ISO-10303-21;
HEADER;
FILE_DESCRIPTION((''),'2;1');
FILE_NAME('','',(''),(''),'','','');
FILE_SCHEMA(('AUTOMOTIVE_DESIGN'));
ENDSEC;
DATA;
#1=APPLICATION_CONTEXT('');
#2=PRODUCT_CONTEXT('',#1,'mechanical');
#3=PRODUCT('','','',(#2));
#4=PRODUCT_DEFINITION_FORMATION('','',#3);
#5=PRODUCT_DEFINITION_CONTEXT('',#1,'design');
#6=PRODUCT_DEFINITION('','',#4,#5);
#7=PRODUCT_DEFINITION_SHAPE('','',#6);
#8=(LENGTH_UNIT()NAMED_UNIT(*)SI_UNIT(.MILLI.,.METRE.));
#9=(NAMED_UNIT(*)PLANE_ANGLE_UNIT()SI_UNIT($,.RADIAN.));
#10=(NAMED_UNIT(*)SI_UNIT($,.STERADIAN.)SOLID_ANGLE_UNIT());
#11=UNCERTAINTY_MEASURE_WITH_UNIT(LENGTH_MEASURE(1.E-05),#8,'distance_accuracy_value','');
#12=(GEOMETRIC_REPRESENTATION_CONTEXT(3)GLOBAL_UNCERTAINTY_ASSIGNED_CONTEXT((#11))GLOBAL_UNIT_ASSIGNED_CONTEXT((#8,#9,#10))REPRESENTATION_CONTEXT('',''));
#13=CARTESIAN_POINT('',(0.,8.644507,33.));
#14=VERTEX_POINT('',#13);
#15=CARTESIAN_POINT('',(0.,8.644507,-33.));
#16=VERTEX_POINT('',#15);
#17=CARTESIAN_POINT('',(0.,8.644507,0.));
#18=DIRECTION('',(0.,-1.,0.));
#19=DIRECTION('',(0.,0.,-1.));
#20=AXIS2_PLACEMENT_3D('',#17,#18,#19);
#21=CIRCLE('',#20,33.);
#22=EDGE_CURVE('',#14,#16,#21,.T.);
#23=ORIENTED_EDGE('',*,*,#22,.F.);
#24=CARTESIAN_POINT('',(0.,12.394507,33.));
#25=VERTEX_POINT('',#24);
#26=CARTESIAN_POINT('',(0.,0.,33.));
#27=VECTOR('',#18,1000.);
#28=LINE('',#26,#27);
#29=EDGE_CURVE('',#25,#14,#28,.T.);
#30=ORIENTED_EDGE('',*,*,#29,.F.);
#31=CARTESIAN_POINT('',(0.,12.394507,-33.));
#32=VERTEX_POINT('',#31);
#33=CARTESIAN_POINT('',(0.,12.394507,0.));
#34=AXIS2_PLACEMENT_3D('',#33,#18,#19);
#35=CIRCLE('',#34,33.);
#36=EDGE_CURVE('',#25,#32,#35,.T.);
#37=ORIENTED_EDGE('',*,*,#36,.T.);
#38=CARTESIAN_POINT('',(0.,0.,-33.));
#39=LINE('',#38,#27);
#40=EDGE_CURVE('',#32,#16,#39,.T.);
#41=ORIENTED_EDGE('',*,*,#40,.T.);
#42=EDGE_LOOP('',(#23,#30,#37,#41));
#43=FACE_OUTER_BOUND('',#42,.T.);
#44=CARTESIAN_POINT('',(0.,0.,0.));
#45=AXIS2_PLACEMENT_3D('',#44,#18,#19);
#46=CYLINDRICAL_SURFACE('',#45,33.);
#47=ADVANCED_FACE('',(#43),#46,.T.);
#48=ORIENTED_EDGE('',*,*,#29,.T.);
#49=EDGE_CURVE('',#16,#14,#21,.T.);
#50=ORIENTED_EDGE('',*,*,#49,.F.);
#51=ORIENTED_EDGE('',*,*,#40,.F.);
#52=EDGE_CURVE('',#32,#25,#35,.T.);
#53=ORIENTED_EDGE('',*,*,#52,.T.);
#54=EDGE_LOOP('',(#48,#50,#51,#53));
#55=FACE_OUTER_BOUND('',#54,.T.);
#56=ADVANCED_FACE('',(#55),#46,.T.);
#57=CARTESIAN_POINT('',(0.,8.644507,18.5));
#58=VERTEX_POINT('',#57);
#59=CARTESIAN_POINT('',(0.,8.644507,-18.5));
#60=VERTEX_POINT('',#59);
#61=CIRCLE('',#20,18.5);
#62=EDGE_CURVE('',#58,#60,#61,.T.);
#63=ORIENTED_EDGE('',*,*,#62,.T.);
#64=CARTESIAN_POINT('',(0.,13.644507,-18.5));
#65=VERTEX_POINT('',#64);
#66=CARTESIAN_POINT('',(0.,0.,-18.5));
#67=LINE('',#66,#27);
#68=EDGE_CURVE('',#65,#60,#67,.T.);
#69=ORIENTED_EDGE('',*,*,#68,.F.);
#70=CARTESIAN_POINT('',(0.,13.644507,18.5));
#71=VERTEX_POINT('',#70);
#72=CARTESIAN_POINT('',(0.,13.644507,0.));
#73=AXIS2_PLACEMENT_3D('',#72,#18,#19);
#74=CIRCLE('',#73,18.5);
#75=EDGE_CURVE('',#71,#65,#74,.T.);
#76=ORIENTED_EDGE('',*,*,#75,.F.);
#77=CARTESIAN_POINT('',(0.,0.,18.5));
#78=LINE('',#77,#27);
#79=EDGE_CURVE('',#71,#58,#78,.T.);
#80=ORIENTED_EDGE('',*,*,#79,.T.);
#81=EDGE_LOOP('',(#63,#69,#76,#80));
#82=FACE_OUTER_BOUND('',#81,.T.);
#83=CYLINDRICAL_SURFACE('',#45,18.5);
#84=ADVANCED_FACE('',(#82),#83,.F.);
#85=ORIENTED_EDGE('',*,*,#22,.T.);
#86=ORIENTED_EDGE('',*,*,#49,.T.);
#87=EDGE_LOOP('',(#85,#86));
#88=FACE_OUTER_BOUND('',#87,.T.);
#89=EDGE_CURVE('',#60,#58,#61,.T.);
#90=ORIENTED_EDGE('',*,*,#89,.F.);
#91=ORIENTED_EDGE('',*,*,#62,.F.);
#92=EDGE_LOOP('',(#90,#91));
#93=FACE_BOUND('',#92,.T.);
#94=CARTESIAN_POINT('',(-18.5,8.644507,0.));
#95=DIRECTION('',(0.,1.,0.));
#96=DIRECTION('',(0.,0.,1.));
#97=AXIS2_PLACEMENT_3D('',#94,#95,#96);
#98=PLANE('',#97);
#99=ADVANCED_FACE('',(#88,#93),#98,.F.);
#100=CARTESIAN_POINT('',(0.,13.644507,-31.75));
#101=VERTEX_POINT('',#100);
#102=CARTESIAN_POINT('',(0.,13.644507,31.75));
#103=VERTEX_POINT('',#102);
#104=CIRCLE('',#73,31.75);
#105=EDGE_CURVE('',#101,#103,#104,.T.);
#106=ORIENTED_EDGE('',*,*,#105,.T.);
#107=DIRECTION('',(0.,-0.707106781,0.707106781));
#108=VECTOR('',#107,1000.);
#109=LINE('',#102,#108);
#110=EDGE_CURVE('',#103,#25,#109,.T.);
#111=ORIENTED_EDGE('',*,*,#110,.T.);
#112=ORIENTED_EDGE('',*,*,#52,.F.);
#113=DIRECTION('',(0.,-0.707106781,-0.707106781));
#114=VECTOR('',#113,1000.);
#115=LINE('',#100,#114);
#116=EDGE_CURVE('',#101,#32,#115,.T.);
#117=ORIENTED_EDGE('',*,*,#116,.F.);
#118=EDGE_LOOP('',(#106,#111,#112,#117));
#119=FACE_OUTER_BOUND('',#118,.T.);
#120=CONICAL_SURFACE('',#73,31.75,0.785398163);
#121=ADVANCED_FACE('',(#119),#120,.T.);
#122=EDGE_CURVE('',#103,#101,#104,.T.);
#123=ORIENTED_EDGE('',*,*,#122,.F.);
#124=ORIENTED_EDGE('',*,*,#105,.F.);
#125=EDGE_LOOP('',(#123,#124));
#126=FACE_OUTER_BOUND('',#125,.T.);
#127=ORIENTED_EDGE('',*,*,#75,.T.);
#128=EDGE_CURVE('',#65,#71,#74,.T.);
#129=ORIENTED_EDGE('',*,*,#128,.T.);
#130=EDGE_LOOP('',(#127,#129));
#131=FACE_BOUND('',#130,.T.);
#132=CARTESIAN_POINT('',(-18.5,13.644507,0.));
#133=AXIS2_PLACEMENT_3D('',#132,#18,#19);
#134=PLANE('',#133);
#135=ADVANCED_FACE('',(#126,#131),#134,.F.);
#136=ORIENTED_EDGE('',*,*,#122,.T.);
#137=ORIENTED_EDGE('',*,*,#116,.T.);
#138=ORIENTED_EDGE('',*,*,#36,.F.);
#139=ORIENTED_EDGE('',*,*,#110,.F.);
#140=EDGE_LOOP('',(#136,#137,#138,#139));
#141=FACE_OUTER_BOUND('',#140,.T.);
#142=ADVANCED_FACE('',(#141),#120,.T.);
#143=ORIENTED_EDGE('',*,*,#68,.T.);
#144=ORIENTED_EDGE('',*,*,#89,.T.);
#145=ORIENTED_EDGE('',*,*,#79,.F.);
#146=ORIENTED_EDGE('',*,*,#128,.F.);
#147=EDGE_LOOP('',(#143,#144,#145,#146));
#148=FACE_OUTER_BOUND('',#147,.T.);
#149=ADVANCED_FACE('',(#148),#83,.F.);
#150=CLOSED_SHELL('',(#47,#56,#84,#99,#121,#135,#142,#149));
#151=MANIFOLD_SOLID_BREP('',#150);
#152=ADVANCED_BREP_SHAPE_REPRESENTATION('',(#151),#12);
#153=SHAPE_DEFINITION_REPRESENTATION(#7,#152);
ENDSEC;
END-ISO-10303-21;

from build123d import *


with BuildPart() as part:
    # 草图1 → Revolve 481 (revolve)
    with BuildSketch(Plane.XY, mode=Mode.PRIVATE) as revolve_481_sk:
        Polygon((-31.75, 13.644507042), (-33, 12.394507042), (-33, 8.644507042), (-18.5, 8.644507042), (-18.5, 13.644507042), align=None)
    revolve(revolve_481_sk.sketch.rotate(Axis((0, 0, 0), (0, 1, 0)), 270), axis=Axis((0, 0, 0), (0, 1, 0)))


solid = part.part
